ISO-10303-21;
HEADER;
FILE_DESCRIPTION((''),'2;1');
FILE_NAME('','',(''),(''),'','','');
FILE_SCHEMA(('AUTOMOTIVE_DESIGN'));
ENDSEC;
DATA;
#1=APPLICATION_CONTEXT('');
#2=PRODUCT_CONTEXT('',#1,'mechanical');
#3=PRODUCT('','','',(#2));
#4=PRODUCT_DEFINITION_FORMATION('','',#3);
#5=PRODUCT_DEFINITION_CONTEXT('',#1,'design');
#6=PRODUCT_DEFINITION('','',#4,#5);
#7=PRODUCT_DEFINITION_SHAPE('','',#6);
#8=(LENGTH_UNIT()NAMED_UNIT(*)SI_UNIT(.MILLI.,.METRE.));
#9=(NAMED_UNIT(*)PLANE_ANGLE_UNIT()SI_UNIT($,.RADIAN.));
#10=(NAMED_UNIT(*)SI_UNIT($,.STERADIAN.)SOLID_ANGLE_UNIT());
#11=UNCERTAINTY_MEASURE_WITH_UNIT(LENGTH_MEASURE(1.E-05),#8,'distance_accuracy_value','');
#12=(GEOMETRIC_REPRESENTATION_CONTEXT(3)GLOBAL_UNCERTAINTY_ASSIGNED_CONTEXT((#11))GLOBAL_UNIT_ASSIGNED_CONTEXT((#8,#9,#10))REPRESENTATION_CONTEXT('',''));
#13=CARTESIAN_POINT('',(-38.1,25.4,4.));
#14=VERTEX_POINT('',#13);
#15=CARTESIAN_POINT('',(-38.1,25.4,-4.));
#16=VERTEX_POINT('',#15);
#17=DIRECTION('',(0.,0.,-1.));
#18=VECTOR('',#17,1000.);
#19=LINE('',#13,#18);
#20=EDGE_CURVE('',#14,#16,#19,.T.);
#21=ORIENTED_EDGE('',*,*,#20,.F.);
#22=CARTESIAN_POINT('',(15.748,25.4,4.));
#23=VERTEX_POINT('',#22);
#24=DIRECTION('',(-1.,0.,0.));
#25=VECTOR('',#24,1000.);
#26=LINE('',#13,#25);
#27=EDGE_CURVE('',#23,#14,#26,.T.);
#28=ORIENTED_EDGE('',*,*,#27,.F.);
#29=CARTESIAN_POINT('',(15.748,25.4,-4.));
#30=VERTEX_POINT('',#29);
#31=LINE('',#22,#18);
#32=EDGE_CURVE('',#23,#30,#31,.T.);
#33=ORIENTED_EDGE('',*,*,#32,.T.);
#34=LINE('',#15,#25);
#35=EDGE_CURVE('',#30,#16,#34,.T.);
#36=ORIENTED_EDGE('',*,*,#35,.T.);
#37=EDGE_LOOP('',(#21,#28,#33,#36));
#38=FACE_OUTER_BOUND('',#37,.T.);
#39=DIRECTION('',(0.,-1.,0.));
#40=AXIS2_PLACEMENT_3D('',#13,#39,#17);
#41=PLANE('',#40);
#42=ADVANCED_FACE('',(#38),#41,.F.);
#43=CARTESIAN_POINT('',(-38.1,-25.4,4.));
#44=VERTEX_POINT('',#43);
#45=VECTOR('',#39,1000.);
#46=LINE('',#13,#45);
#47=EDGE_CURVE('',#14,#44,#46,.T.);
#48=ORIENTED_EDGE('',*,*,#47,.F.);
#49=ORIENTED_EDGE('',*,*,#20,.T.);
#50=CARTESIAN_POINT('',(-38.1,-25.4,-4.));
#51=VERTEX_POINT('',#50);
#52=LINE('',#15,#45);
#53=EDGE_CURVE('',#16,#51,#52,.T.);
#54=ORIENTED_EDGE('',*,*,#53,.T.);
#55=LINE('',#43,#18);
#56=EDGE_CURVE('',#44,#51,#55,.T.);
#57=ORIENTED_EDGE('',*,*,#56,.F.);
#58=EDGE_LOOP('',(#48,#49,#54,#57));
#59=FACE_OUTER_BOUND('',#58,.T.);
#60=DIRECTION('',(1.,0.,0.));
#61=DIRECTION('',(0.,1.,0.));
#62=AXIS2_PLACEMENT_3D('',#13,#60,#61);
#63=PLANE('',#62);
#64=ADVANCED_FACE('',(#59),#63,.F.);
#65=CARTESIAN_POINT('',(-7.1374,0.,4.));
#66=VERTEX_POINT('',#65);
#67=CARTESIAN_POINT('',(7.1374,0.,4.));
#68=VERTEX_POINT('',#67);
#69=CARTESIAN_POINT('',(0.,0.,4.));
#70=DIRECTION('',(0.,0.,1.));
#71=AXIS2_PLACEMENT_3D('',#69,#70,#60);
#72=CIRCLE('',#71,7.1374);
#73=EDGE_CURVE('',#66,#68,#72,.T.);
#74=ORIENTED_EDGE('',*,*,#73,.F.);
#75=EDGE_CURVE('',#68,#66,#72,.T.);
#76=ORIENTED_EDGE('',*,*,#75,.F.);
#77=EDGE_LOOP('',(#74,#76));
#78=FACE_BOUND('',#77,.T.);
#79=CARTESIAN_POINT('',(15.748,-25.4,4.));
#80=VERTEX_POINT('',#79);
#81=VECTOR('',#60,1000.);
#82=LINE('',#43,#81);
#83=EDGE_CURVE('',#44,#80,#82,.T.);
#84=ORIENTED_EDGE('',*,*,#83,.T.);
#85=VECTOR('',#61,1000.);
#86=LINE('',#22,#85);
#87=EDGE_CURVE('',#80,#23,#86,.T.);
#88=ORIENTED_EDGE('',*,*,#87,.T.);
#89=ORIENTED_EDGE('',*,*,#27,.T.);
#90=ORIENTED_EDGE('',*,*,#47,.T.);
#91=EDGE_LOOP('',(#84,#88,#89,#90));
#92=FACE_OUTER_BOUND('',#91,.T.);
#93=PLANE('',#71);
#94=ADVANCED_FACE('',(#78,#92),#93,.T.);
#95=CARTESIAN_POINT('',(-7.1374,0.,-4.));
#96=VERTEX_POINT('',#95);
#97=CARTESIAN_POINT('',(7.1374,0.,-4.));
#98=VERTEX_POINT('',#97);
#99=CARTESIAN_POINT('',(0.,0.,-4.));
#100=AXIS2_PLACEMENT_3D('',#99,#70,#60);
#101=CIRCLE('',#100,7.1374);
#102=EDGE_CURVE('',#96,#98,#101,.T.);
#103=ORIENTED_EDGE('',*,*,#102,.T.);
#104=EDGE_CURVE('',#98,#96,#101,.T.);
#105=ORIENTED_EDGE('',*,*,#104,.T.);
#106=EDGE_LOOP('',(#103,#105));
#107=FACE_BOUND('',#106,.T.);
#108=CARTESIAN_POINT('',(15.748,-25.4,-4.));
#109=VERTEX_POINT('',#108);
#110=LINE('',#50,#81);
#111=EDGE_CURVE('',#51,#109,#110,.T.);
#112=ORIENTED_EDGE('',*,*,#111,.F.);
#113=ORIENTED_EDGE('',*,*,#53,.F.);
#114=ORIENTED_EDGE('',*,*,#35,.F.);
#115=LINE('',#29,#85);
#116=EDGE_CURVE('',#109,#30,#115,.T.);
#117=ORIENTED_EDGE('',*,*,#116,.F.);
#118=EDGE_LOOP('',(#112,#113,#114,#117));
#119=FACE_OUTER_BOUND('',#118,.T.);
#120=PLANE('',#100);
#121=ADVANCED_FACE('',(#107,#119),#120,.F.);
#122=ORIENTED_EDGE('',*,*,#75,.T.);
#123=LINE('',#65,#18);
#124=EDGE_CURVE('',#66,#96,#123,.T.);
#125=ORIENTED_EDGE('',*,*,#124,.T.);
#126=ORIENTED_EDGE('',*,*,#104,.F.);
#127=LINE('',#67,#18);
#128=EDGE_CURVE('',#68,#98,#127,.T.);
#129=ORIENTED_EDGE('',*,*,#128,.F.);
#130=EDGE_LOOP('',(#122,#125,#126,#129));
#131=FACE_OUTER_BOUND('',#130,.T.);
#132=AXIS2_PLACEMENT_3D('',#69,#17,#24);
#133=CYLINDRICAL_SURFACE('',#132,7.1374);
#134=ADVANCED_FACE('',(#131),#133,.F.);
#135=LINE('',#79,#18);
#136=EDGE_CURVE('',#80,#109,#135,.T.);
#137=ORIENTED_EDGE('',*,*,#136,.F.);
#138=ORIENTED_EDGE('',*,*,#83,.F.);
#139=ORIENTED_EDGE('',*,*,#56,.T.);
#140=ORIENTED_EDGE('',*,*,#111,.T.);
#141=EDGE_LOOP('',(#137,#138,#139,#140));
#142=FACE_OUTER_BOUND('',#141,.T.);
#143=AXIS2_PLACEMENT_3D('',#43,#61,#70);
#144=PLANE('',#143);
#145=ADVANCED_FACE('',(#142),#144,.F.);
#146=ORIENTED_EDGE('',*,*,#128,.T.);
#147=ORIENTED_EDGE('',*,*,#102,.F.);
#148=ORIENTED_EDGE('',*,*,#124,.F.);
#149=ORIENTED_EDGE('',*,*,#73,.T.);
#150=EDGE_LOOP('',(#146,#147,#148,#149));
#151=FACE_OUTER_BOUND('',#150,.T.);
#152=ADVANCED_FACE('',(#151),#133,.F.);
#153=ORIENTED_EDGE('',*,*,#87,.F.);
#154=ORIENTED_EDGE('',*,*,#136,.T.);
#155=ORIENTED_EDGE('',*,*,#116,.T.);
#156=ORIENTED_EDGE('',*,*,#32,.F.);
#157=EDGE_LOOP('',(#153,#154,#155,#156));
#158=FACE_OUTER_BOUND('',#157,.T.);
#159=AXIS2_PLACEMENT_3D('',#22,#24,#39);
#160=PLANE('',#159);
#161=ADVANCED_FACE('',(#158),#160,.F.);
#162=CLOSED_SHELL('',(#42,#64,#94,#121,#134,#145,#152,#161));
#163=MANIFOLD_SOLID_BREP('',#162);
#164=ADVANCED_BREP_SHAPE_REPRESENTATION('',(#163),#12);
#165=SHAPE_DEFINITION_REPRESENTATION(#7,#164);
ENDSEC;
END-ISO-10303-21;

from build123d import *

# Parameters (mm, degrees)
SKETCH1_W           = 53.848
SKETCH1_H           = 50.8
SKETCH1_R           = 7.1374
BOSS_EXTRUDE1_DEPTH = 4


with BuildPart() as part:
    # Sketch1 → Boss-Extrude1 (new, symmetric)
    with BuildSketch(Plane.XY):
        with Locations((-11.176, 0)):
            Rectangle(SKETCH1_W, SKETCH1_H)
        Circle(SKETCH1_R, mode=Mode.SUBTRACT)
    extrude(amount=BOSS_EXTRUDE1_DEPTH, both=True)


solid = part.part
